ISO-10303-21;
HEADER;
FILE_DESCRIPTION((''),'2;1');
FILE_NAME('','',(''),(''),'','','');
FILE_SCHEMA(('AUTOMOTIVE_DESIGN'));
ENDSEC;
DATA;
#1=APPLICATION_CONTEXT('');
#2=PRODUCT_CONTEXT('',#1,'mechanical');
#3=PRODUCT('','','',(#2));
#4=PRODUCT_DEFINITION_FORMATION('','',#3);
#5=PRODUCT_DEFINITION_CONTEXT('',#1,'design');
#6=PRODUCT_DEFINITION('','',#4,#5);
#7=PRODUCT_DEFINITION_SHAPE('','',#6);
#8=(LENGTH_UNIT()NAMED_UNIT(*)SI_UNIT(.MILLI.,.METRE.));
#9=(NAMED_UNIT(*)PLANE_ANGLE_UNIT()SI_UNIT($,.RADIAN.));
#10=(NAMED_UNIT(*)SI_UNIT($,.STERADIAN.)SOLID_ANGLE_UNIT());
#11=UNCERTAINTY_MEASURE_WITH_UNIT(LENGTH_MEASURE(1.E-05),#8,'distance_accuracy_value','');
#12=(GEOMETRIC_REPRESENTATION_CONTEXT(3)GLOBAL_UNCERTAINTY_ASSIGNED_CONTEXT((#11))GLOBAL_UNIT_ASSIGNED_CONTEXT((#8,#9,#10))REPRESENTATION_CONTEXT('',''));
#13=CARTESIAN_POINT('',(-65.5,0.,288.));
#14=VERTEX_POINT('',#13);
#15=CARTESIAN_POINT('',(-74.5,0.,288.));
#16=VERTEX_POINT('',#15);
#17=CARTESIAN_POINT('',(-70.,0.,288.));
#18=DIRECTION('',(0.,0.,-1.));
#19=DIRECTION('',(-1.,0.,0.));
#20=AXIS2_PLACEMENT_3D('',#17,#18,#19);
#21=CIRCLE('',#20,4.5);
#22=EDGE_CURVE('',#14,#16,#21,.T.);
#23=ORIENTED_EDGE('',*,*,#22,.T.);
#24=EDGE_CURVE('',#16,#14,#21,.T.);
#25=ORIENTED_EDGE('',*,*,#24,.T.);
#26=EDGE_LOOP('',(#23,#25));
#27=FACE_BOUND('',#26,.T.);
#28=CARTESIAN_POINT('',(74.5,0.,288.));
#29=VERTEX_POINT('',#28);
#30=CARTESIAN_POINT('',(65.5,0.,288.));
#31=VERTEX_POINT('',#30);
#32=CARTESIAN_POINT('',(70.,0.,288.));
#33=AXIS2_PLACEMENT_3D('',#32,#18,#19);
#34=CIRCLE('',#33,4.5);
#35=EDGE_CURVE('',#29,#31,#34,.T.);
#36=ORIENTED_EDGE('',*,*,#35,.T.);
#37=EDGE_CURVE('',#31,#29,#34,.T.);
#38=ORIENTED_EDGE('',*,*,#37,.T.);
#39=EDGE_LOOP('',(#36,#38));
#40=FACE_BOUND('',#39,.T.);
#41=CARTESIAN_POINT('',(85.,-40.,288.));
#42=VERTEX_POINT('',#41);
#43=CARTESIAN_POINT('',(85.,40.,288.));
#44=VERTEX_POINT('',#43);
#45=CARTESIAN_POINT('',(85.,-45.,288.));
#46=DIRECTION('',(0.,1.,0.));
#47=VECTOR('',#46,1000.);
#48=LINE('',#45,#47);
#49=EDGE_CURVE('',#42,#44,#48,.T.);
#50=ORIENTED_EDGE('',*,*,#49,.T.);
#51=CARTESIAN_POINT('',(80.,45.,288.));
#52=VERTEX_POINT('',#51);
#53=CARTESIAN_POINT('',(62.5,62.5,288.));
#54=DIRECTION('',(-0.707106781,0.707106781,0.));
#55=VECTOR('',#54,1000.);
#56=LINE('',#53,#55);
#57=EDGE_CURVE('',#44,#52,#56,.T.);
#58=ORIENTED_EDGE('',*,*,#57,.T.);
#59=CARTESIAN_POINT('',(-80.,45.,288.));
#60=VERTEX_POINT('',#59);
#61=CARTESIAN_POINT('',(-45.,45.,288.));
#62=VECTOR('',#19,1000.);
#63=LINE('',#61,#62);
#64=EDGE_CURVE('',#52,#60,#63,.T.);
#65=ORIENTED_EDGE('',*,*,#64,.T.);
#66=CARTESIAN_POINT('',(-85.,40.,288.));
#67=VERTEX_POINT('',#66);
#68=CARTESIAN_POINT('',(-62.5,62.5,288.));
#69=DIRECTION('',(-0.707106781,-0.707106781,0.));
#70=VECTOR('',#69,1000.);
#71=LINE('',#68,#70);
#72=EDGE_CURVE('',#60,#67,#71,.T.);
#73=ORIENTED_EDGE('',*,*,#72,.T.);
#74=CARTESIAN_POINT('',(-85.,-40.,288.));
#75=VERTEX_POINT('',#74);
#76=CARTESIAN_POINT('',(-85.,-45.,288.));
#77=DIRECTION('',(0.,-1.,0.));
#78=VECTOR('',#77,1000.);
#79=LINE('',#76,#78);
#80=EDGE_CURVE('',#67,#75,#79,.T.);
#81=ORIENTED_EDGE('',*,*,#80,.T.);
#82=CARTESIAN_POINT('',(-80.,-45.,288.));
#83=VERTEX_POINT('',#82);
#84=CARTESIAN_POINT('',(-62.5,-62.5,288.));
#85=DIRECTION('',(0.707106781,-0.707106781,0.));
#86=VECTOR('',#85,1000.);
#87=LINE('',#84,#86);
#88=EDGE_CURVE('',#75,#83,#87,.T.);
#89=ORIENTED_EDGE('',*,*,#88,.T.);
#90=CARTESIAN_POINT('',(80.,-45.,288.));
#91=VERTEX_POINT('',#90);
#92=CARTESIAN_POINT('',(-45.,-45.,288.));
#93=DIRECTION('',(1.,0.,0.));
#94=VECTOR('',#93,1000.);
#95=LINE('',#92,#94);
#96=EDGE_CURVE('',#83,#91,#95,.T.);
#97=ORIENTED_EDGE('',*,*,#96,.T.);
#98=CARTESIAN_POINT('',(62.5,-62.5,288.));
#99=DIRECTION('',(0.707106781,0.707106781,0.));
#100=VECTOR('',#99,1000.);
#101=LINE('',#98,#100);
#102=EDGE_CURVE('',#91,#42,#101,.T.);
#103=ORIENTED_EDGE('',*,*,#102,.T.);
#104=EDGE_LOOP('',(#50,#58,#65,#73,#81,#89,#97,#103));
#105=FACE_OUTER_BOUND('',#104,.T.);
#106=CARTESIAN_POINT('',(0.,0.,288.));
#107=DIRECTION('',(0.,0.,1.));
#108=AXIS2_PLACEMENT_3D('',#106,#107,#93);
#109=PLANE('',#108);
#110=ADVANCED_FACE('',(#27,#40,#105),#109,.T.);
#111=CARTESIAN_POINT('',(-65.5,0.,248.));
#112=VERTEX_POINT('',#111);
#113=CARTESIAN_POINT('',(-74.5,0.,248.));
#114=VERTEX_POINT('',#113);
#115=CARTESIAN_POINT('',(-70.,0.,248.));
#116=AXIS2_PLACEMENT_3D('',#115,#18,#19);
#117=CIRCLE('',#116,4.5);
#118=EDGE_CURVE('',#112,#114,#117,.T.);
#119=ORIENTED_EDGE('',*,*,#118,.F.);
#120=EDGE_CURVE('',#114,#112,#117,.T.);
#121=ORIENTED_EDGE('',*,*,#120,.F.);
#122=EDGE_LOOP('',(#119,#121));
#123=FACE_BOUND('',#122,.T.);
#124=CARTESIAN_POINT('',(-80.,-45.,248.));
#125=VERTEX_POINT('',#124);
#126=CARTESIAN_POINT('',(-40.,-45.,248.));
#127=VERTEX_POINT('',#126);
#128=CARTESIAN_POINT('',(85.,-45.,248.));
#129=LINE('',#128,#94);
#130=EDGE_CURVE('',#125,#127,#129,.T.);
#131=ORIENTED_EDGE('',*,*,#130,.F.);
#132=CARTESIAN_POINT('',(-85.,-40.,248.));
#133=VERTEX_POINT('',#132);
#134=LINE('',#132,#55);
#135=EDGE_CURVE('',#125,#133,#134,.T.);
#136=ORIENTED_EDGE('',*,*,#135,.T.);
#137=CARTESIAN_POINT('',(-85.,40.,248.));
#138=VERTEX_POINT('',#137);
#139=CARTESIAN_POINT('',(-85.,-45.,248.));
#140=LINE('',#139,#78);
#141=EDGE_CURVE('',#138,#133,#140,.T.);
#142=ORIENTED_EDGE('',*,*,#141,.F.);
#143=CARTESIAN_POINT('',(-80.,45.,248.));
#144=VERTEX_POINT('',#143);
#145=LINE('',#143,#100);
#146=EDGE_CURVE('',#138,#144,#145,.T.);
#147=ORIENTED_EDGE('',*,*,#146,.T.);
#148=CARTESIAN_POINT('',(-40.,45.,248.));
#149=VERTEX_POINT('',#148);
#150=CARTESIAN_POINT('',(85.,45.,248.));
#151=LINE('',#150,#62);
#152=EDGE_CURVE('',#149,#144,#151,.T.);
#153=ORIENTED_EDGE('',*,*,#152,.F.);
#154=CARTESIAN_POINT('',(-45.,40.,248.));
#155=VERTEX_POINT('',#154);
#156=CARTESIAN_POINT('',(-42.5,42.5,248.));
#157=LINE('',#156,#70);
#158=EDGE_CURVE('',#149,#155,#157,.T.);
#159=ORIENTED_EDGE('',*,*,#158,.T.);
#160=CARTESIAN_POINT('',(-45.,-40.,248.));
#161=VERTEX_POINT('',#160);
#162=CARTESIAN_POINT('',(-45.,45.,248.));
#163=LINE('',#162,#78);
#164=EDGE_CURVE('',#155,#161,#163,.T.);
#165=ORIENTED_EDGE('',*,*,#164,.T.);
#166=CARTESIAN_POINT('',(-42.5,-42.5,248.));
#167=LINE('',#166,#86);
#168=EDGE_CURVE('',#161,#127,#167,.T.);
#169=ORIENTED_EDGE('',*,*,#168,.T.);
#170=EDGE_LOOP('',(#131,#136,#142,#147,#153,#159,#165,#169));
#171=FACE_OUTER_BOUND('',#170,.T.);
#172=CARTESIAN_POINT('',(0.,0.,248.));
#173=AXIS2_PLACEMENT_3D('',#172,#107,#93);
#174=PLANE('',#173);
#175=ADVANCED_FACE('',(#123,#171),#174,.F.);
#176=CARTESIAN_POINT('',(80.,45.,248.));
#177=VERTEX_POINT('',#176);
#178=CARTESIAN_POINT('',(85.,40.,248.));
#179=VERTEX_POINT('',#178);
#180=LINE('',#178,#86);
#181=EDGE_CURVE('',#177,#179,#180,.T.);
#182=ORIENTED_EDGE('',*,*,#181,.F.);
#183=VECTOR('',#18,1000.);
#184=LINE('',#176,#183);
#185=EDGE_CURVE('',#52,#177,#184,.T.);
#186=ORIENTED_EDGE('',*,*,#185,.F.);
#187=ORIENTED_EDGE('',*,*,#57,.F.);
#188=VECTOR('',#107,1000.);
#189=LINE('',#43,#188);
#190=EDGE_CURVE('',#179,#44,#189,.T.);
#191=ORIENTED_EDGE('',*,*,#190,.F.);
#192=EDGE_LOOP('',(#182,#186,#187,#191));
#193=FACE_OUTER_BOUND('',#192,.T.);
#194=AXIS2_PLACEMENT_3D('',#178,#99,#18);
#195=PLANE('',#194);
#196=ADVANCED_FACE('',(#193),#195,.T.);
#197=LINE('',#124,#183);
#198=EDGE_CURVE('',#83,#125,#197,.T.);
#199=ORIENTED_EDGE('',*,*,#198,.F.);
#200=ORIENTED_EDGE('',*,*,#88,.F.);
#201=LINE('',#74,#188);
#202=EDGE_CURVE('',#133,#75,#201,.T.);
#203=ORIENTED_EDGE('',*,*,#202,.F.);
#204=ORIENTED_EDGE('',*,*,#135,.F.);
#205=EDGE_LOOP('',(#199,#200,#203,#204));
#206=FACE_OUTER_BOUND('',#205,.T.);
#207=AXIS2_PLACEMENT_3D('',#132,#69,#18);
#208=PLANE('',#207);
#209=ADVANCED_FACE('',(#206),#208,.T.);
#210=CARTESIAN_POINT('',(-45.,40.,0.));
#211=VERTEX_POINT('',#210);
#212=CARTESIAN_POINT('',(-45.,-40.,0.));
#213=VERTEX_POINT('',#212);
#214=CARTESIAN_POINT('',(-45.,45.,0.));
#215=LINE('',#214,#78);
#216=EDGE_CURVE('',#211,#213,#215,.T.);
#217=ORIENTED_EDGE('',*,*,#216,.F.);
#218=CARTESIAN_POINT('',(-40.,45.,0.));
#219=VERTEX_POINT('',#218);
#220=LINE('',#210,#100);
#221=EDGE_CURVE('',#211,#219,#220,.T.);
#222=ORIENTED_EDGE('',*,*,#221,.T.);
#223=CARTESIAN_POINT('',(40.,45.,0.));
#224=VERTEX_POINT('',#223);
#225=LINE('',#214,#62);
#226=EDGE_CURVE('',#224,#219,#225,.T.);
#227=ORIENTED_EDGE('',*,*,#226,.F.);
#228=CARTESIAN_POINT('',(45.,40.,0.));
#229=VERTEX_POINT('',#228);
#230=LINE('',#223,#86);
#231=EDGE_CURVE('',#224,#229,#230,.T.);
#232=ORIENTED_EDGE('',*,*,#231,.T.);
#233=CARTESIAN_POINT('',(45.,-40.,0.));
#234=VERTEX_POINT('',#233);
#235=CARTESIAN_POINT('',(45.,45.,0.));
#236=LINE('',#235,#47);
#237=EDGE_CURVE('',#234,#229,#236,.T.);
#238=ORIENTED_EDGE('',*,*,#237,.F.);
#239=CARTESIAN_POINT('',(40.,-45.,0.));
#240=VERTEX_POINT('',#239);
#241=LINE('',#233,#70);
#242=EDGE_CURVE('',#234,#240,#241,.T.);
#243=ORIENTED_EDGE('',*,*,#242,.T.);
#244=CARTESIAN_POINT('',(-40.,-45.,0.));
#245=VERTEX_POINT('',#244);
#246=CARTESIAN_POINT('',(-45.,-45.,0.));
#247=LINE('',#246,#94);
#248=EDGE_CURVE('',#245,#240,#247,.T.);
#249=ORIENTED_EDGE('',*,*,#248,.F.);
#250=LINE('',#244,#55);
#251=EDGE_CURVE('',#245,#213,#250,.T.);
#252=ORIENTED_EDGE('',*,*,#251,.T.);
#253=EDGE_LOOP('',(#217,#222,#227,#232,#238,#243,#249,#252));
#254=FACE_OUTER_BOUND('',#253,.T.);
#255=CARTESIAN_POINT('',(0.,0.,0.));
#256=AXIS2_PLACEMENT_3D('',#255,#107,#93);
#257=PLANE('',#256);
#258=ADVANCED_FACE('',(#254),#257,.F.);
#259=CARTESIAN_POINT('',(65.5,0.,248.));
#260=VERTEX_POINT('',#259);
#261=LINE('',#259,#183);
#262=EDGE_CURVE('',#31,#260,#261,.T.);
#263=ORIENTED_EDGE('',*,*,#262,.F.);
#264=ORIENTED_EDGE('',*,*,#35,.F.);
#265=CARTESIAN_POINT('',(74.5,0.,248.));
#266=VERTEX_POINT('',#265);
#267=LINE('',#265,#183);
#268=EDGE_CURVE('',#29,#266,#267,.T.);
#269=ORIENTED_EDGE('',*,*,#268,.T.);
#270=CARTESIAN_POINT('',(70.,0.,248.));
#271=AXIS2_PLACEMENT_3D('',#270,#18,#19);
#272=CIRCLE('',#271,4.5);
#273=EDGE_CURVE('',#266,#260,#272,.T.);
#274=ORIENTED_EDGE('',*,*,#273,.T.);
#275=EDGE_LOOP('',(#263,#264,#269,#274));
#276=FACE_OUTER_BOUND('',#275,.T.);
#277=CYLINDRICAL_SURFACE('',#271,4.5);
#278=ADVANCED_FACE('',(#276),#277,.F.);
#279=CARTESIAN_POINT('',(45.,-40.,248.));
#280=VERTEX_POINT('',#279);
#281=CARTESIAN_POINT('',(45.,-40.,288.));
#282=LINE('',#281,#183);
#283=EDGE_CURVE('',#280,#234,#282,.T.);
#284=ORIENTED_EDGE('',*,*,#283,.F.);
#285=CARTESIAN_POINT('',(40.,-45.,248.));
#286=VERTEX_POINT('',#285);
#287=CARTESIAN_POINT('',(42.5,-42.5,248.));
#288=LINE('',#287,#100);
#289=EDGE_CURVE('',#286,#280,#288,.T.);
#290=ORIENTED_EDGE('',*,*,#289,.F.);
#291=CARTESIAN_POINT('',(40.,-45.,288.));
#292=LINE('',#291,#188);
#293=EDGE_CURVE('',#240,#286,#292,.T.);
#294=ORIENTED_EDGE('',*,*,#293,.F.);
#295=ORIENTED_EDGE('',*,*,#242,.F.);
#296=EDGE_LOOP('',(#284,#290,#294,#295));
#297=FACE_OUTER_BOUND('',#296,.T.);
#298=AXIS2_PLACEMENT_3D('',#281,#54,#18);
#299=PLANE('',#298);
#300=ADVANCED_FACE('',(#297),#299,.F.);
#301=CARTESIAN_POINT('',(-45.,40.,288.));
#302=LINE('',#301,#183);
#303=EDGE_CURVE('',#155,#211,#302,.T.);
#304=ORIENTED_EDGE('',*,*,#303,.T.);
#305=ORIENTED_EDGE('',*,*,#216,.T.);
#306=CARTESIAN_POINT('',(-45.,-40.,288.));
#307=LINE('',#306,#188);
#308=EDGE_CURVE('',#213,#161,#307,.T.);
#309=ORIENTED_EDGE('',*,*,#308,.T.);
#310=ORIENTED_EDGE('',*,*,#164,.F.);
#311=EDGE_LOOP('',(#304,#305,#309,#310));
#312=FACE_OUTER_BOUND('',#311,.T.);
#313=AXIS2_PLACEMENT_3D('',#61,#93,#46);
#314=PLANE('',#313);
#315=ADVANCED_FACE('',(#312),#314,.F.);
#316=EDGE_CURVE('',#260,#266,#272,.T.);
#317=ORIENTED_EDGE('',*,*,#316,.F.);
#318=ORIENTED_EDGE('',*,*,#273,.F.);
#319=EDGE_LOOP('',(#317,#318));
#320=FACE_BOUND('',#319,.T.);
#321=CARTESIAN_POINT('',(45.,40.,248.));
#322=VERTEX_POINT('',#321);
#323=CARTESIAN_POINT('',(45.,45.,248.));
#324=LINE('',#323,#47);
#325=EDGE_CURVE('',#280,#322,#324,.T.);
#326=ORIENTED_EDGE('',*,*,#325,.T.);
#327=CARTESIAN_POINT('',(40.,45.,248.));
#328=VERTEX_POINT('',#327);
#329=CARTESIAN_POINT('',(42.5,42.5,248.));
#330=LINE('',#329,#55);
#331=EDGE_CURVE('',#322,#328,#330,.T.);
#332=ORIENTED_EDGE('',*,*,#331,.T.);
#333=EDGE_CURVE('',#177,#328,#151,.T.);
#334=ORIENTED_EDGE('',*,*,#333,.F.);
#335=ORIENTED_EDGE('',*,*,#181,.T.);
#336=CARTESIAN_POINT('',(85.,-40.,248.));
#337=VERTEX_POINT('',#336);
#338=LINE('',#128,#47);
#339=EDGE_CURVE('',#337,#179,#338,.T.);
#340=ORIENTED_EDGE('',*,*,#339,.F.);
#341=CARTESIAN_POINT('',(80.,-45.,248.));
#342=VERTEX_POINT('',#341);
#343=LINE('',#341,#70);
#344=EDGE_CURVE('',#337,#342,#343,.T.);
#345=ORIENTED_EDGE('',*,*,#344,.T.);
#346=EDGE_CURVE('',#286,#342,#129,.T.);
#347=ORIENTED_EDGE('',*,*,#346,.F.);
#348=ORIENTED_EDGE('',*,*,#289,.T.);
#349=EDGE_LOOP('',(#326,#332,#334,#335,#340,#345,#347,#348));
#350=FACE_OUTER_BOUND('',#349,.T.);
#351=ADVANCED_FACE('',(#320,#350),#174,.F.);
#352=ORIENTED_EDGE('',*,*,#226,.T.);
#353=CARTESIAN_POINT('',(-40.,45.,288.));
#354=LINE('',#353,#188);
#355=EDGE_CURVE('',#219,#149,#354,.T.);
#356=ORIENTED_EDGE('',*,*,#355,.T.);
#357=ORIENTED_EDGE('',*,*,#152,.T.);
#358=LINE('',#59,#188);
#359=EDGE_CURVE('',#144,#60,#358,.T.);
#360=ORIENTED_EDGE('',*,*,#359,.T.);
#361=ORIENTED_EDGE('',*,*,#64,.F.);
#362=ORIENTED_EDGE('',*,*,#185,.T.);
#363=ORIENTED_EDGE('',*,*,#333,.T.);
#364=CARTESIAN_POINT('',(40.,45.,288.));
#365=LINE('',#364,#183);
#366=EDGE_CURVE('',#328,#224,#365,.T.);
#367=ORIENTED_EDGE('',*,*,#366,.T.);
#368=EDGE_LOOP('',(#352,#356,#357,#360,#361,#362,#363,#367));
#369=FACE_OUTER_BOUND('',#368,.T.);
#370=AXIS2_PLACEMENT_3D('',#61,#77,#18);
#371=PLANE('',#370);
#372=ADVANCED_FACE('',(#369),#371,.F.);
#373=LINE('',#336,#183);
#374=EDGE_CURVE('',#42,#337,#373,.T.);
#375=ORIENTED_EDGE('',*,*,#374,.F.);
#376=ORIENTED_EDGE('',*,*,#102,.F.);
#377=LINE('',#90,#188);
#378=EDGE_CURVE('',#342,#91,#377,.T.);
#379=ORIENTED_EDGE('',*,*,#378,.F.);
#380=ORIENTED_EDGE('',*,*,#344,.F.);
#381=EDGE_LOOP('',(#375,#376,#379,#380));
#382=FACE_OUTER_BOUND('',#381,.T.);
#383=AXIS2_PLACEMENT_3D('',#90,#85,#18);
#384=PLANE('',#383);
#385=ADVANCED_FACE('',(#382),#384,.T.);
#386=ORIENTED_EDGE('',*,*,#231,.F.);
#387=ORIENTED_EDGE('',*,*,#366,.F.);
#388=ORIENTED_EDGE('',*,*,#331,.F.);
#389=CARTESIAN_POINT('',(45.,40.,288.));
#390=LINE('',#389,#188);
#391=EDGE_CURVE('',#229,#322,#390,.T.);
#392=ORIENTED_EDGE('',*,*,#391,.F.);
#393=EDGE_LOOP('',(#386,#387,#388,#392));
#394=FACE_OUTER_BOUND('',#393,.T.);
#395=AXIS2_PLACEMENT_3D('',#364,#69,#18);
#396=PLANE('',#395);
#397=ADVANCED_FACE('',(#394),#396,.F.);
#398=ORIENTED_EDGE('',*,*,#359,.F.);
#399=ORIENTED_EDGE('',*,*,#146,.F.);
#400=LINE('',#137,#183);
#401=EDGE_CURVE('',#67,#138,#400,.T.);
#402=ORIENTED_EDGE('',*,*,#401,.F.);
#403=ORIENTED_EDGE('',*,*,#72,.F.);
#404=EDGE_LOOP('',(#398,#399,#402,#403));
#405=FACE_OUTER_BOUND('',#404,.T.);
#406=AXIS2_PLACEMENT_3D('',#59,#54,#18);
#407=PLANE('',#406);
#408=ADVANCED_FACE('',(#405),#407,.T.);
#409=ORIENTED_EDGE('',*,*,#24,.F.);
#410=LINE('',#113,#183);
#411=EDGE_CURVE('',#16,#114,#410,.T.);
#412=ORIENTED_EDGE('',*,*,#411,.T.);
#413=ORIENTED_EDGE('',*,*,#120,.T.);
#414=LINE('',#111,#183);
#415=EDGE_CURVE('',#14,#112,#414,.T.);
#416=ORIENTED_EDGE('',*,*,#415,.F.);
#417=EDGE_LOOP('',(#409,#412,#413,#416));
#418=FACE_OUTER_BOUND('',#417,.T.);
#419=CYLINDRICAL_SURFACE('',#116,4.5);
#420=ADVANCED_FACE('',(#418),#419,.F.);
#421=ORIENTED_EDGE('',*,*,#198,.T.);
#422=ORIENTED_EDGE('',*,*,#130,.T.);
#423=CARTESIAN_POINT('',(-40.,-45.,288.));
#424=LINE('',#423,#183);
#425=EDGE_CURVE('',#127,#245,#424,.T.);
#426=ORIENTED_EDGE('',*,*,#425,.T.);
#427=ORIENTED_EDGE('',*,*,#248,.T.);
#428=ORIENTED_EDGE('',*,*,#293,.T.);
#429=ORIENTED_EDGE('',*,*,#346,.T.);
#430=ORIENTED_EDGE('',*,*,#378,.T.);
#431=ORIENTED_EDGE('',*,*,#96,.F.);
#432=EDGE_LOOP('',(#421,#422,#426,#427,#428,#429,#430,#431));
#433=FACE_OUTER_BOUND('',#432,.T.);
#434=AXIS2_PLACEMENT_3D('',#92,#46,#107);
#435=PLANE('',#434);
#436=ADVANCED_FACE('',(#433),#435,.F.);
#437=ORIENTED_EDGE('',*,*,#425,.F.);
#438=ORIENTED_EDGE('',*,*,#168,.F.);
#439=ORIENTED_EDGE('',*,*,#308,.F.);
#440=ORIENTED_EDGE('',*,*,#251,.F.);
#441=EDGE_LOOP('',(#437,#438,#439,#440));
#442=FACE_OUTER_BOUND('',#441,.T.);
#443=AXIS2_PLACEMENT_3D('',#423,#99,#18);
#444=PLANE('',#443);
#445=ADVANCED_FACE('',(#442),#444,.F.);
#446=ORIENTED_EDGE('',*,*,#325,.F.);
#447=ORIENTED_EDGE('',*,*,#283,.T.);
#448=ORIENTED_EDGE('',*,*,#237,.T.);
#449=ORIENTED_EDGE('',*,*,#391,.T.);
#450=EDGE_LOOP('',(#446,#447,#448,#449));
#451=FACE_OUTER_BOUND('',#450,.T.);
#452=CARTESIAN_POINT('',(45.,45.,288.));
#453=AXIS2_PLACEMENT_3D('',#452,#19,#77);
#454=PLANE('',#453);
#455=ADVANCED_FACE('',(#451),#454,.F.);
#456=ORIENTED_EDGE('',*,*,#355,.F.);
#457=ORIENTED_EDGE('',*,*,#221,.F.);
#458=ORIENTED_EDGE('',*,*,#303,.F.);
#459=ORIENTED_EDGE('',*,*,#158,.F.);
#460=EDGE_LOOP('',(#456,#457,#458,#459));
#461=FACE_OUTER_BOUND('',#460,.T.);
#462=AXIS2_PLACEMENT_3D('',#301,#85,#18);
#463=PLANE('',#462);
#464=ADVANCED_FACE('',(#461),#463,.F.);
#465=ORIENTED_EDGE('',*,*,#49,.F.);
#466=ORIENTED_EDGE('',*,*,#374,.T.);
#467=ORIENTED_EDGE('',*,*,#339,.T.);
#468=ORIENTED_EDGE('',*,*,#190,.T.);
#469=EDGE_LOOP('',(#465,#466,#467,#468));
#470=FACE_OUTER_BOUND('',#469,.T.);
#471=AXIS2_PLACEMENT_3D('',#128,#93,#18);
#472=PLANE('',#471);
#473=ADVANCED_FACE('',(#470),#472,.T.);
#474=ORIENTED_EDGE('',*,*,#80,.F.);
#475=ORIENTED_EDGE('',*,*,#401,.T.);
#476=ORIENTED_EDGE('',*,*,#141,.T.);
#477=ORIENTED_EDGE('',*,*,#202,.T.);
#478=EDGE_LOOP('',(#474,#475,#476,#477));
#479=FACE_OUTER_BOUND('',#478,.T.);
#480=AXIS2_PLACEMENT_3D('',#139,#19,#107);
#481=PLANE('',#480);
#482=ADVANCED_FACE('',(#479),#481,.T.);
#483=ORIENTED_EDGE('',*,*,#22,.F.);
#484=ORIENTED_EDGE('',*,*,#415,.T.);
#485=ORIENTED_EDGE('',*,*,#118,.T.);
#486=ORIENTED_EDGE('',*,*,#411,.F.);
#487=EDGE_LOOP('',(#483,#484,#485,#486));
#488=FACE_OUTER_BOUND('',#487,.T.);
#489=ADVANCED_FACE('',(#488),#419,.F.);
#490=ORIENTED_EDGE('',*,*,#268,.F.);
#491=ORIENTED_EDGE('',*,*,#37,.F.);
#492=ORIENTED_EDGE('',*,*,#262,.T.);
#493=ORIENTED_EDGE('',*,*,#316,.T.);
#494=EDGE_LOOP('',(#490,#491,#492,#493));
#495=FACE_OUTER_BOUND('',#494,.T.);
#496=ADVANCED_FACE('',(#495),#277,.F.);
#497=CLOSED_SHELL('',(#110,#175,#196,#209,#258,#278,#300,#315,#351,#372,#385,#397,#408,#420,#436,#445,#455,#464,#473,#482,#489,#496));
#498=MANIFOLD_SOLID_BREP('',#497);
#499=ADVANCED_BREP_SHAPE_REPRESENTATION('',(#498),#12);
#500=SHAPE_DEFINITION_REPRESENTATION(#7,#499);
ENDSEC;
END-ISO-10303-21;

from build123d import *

# Parameters (mm, degrees)
SKETCH1_W            = 90
SKETCH1_H            = 90
BOSS_EXTRUDE1_DEPTH  = 288
SKETCH2_W            = 170
SKETCH2_H            = 90
BOSS_EXTRUDE2_DEPTH  = 40
CHAMFER1_SIZE        = 5
M8_CLEARANCE_HOLE1_D = 9


with BuildPart() as part:
    # Sketch1 → Boss-Extrude1 (new body)
    with BuildSketch(Plane.XY):
        Rectangle(SKETCH1_W, SKETCH1_H)
    extrude(amount=BOSS_EXTRUDE1_DEPTH)

    # Sketch2 → Boss-Extrude2 (add)
    with BuildSketch(Plane.XY.offset(288)):
        Rectangle(SKETCH2_W, SKETCH2_H)
    extrude(amount=-BOSS_EXTRUDE2_DEPTH)

    # Chamfer1
    chamfer1_edges = [part.edges().sort_by_distance(p)[0] for p in [
        (45, -45, 124),
        (-45, -45, 124),
        (-45, 45, 124),
        (45, 45, 124),
        (-85, 45, 268),
        (85, -45, 268),
        (-85, -45, 268),
        (85, 45, 268),
    ]]
    chamfer(chamfer1_edges, length=CHAMFER1_SIZE)

    # M8 Clearance Hole1 (through all)
    with Locations(Plane(origin=(0, 0, 248), x_dir=(-1, 0, 0), z_dir=(0, 0, -1))):
        with Locations((-70, 0), (70, 0)):
            Hole(M8_CLEARANCE_HOLE1_D / 2)


solid = part.part
